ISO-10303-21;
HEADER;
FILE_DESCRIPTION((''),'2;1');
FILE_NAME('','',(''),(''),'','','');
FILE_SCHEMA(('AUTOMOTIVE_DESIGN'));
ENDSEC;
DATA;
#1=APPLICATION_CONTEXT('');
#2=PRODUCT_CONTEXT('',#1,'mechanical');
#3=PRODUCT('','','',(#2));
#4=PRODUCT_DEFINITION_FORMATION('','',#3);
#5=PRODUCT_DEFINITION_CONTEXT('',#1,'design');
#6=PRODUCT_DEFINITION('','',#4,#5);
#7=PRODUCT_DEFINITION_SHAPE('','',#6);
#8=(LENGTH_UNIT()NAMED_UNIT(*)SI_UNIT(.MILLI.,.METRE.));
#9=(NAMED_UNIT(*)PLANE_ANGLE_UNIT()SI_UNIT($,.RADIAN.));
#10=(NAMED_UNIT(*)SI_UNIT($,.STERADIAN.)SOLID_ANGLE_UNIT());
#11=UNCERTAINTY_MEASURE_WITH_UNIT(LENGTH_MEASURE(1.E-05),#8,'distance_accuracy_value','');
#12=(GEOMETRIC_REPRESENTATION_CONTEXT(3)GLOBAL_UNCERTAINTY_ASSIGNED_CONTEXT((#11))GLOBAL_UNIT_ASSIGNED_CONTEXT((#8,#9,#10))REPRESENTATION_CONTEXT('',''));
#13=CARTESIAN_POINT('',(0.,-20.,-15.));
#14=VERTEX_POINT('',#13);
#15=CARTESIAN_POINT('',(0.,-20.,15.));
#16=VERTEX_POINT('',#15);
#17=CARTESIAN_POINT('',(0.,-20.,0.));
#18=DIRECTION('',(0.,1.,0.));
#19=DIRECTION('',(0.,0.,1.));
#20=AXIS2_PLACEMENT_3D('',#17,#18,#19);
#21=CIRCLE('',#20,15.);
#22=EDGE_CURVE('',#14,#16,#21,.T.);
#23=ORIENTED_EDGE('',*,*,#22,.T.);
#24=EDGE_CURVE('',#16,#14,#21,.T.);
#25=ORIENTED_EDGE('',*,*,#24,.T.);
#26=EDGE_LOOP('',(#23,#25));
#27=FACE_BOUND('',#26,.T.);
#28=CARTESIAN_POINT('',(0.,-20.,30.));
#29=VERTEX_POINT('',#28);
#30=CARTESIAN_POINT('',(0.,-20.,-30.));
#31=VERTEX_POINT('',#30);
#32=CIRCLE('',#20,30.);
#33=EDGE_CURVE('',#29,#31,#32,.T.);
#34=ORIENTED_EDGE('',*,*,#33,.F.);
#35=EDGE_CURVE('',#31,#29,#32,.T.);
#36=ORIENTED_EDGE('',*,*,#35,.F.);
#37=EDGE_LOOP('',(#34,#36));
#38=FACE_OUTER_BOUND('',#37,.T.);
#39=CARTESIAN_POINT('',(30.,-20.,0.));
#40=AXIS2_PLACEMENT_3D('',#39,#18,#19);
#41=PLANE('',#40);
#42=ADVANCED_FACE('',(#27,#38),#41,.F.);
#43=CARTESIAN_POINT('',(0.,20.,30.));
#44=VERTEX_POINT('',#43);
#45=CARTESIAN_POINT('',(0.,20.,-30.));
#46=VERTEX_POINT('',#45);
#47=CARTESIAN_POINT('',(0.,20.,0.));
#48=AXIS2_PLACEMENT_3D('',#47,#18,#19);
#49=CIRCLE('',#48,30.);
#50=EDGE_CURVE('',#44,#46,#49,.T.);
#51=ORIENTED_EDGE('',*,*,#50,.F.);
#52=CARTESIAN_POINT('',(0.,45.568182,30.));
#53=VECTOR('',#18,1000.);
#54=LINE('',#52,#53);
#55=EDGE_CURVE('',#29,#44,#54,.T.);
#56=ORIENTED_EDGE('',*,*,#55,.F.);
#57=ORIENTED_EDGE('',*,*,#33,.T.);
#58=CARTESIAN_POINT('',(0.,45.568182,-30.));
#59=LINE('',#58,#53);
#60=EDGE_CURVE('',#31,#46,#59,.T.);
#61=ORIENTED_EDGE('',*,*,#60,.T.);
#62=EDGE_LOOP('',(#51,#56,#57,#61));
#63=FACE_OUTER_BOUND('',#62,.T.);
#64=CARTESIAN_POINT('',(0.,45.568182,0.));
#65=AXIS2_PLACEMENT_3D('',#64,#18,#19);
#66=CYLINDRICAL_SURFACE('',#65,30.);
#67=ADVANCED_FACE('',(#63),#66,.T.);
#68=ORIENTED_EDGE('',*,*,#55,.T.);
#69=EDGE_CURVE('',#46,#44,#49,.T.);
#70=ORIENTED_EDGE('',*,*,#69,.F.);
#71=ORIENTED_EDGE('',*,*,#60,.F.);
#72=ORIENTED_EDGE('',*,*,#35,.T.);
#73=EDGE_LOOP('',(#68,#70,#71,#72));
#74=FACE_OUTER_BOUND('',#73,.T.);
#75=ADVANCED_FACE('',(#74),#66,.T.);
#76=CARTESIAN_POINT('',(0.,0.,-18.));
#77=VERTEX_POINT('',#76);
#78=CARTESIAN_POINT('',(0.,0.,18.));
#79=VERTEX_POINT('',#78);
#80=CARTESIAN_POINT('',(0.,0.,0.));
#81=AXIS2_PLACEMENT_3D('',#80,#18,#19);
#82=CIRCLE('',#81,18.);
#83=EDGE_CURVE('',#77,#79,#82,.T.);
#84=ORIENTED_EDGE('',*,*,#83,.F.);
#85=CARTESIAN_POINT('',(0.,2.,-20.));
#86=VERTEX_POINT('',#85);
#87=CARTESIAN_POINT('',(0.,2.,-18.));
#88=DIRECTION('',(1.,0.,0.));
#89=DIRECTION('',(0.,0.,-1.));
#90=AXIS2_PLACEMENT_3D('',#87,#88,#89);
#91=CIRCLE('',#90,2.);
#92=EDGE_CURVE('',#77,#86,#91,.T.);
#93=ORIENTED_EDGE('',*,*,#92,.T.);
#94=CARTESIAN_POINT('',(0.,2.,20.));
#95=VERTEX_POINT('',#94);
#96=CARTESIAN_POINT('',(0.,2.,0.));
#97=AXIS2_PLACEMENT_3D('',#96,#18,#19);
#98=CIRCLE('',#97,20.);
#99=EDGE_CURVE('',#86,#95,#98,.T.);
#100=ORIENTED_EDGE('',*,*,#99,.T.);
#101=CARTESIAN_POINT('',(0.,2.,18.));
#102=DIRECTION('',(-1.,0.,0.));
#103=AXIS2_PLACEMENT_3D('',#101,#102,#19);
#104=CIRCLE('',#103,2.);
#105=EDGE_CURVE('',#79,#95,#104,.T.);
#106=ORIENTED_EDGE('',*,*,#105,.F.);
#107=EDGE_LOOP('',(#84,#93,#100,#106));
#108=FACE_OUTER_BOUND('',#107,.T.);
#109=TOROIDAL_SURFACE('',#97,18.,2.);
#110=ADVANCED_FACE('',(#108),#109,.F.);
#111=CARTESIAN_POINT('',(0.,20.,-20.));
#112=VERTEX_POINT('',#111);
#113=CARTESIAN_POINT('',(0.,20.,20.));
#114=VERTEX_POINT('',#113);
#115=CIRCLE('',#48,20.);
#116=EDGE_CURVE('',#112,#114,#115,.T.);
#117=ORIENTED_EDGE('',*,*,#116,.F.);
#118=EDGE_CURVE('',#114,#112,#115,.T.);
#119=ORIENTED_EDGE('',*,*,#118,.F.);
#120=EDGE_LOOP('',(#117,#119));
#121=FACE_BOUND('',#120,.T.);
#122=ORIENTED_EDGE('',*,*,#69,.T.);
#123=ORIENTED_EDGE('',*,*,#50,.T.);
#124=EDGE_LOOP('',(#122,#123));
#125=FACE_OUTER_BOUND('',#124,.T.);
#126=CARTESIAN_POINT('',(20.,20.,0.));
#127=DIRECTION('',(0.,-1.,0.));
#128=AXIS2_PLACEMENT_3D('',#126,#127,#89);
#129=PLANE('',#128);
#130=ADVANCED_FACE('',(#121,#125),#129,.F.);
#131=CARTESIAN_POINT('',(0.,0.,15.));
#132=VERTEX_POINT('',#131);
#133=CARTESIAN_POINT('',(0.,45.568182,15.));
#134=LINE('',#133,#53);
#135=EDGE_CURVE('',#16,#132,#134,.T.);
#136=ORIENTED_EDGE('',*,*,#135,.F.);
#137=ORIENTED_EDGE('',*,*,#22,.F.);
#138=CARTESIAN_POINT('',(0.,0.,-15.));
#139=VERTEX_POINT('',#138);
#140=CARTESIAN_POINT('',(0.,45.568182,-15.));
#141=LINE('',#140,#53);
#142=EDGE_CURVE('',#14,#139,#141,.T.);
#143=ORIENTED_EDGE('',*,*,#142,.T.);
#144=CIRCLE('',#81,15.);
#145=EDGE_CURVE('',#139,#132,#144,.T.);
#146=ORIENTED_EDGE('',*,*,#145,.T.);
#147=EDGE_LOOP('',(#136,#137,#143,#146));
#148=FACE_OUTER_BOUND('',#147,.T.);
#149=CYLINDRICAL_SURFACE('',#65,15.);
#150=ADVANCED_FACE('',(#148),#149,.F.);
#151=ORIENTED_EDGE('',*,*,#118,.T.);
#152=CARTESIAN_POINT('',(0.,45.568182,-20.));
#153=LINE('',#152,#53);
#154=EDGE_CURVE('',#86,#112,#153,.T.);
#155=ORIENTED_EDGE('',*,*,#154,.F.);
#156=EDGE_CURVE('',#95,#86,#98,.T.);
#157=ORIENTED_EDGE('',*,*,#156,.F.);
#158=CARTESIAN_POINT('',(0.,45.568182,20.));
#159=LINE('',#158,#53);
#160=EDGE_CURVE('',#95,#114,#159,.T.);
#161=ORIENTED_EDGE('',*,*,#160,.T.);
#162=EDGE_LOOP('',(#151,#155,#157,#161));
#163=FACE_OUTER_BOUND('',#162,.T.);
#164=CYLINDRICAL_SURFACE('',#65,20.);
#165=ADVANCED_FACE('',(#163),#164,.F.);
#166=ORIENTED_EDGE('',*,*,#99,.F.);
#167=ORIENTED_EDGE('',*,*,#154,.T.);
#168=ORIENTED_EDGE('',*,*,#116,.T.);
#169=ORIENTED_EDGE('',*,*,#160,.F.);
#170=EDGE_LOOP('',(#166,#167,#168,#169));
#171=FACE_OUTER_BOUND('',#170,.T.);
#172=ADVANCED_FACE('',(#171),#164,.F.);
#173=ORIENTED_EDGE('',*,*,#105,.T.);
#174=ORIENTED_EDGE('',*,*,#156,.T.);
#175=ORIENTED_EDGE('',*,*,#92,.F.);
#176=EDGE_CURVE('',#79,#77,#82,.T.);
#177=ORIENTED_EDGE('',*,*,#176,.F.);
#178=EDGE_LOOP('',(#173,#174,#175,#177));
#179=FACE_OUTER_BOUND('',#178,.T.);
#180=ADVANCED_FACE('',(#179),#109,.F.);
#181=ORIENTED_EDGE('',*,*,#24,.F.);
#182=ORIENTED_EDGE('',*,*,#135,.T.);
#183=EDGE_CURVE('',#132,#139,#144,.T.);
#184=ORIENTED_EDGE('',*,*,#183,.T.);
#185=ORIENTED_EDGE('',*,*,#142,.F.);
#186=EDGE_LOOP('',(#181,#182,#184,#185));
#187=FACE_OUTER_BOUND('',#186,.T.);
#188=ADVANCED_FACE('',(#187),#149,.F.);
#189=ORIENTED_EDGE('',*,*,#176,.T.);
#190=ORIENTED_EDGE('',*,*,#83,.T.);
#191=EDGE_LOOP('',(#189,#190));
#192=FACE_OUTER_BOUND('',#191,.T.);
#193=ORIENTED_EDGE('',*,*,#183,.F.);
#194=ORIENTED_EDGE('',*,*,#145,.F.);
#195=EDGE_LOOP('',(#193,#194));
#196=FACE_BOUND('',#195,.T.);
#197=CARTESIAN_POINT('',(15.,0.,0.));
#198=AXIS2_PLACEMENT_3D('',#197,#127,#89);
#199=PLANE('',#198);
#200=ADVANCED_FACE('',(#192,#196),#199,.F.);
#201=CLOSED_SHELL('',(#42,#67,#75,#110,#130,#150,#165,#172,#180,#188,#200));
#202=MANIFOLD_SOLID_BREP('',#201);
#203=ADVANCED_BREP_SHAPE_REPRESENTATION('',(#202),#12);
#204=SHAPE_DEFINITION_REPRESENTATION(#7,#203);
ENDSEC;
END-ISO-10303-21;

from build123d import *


with BuildPart() as part:
    # 草图1 → 旋转1 (revolve)
    with BuildSketch(Plane.XY, mode=Mode.PRIVATE) as revolve_1_sk:
        with BuildLine():
            Line((15, -20), (15, 0))
            Line((15, 0), (18, 0))
            ThreePointArc((18, 0), (19.414213562, 0.585786438), (20, 2))
            Line((20, 2), (20, 20))
            Line((20, 20), (30, 20))
            Line((30, 20), (30, -20))
            Line((30, -20), (15, -20))
        make_face()
    revolve(revolve_1_sk.sketch.rotate(Axis((0, 45.568181818, 0), (0, -1, 0)), 90), axis=Axis((0, 45.568181818, 0), (0, -1, 0)))


solid = part.part
